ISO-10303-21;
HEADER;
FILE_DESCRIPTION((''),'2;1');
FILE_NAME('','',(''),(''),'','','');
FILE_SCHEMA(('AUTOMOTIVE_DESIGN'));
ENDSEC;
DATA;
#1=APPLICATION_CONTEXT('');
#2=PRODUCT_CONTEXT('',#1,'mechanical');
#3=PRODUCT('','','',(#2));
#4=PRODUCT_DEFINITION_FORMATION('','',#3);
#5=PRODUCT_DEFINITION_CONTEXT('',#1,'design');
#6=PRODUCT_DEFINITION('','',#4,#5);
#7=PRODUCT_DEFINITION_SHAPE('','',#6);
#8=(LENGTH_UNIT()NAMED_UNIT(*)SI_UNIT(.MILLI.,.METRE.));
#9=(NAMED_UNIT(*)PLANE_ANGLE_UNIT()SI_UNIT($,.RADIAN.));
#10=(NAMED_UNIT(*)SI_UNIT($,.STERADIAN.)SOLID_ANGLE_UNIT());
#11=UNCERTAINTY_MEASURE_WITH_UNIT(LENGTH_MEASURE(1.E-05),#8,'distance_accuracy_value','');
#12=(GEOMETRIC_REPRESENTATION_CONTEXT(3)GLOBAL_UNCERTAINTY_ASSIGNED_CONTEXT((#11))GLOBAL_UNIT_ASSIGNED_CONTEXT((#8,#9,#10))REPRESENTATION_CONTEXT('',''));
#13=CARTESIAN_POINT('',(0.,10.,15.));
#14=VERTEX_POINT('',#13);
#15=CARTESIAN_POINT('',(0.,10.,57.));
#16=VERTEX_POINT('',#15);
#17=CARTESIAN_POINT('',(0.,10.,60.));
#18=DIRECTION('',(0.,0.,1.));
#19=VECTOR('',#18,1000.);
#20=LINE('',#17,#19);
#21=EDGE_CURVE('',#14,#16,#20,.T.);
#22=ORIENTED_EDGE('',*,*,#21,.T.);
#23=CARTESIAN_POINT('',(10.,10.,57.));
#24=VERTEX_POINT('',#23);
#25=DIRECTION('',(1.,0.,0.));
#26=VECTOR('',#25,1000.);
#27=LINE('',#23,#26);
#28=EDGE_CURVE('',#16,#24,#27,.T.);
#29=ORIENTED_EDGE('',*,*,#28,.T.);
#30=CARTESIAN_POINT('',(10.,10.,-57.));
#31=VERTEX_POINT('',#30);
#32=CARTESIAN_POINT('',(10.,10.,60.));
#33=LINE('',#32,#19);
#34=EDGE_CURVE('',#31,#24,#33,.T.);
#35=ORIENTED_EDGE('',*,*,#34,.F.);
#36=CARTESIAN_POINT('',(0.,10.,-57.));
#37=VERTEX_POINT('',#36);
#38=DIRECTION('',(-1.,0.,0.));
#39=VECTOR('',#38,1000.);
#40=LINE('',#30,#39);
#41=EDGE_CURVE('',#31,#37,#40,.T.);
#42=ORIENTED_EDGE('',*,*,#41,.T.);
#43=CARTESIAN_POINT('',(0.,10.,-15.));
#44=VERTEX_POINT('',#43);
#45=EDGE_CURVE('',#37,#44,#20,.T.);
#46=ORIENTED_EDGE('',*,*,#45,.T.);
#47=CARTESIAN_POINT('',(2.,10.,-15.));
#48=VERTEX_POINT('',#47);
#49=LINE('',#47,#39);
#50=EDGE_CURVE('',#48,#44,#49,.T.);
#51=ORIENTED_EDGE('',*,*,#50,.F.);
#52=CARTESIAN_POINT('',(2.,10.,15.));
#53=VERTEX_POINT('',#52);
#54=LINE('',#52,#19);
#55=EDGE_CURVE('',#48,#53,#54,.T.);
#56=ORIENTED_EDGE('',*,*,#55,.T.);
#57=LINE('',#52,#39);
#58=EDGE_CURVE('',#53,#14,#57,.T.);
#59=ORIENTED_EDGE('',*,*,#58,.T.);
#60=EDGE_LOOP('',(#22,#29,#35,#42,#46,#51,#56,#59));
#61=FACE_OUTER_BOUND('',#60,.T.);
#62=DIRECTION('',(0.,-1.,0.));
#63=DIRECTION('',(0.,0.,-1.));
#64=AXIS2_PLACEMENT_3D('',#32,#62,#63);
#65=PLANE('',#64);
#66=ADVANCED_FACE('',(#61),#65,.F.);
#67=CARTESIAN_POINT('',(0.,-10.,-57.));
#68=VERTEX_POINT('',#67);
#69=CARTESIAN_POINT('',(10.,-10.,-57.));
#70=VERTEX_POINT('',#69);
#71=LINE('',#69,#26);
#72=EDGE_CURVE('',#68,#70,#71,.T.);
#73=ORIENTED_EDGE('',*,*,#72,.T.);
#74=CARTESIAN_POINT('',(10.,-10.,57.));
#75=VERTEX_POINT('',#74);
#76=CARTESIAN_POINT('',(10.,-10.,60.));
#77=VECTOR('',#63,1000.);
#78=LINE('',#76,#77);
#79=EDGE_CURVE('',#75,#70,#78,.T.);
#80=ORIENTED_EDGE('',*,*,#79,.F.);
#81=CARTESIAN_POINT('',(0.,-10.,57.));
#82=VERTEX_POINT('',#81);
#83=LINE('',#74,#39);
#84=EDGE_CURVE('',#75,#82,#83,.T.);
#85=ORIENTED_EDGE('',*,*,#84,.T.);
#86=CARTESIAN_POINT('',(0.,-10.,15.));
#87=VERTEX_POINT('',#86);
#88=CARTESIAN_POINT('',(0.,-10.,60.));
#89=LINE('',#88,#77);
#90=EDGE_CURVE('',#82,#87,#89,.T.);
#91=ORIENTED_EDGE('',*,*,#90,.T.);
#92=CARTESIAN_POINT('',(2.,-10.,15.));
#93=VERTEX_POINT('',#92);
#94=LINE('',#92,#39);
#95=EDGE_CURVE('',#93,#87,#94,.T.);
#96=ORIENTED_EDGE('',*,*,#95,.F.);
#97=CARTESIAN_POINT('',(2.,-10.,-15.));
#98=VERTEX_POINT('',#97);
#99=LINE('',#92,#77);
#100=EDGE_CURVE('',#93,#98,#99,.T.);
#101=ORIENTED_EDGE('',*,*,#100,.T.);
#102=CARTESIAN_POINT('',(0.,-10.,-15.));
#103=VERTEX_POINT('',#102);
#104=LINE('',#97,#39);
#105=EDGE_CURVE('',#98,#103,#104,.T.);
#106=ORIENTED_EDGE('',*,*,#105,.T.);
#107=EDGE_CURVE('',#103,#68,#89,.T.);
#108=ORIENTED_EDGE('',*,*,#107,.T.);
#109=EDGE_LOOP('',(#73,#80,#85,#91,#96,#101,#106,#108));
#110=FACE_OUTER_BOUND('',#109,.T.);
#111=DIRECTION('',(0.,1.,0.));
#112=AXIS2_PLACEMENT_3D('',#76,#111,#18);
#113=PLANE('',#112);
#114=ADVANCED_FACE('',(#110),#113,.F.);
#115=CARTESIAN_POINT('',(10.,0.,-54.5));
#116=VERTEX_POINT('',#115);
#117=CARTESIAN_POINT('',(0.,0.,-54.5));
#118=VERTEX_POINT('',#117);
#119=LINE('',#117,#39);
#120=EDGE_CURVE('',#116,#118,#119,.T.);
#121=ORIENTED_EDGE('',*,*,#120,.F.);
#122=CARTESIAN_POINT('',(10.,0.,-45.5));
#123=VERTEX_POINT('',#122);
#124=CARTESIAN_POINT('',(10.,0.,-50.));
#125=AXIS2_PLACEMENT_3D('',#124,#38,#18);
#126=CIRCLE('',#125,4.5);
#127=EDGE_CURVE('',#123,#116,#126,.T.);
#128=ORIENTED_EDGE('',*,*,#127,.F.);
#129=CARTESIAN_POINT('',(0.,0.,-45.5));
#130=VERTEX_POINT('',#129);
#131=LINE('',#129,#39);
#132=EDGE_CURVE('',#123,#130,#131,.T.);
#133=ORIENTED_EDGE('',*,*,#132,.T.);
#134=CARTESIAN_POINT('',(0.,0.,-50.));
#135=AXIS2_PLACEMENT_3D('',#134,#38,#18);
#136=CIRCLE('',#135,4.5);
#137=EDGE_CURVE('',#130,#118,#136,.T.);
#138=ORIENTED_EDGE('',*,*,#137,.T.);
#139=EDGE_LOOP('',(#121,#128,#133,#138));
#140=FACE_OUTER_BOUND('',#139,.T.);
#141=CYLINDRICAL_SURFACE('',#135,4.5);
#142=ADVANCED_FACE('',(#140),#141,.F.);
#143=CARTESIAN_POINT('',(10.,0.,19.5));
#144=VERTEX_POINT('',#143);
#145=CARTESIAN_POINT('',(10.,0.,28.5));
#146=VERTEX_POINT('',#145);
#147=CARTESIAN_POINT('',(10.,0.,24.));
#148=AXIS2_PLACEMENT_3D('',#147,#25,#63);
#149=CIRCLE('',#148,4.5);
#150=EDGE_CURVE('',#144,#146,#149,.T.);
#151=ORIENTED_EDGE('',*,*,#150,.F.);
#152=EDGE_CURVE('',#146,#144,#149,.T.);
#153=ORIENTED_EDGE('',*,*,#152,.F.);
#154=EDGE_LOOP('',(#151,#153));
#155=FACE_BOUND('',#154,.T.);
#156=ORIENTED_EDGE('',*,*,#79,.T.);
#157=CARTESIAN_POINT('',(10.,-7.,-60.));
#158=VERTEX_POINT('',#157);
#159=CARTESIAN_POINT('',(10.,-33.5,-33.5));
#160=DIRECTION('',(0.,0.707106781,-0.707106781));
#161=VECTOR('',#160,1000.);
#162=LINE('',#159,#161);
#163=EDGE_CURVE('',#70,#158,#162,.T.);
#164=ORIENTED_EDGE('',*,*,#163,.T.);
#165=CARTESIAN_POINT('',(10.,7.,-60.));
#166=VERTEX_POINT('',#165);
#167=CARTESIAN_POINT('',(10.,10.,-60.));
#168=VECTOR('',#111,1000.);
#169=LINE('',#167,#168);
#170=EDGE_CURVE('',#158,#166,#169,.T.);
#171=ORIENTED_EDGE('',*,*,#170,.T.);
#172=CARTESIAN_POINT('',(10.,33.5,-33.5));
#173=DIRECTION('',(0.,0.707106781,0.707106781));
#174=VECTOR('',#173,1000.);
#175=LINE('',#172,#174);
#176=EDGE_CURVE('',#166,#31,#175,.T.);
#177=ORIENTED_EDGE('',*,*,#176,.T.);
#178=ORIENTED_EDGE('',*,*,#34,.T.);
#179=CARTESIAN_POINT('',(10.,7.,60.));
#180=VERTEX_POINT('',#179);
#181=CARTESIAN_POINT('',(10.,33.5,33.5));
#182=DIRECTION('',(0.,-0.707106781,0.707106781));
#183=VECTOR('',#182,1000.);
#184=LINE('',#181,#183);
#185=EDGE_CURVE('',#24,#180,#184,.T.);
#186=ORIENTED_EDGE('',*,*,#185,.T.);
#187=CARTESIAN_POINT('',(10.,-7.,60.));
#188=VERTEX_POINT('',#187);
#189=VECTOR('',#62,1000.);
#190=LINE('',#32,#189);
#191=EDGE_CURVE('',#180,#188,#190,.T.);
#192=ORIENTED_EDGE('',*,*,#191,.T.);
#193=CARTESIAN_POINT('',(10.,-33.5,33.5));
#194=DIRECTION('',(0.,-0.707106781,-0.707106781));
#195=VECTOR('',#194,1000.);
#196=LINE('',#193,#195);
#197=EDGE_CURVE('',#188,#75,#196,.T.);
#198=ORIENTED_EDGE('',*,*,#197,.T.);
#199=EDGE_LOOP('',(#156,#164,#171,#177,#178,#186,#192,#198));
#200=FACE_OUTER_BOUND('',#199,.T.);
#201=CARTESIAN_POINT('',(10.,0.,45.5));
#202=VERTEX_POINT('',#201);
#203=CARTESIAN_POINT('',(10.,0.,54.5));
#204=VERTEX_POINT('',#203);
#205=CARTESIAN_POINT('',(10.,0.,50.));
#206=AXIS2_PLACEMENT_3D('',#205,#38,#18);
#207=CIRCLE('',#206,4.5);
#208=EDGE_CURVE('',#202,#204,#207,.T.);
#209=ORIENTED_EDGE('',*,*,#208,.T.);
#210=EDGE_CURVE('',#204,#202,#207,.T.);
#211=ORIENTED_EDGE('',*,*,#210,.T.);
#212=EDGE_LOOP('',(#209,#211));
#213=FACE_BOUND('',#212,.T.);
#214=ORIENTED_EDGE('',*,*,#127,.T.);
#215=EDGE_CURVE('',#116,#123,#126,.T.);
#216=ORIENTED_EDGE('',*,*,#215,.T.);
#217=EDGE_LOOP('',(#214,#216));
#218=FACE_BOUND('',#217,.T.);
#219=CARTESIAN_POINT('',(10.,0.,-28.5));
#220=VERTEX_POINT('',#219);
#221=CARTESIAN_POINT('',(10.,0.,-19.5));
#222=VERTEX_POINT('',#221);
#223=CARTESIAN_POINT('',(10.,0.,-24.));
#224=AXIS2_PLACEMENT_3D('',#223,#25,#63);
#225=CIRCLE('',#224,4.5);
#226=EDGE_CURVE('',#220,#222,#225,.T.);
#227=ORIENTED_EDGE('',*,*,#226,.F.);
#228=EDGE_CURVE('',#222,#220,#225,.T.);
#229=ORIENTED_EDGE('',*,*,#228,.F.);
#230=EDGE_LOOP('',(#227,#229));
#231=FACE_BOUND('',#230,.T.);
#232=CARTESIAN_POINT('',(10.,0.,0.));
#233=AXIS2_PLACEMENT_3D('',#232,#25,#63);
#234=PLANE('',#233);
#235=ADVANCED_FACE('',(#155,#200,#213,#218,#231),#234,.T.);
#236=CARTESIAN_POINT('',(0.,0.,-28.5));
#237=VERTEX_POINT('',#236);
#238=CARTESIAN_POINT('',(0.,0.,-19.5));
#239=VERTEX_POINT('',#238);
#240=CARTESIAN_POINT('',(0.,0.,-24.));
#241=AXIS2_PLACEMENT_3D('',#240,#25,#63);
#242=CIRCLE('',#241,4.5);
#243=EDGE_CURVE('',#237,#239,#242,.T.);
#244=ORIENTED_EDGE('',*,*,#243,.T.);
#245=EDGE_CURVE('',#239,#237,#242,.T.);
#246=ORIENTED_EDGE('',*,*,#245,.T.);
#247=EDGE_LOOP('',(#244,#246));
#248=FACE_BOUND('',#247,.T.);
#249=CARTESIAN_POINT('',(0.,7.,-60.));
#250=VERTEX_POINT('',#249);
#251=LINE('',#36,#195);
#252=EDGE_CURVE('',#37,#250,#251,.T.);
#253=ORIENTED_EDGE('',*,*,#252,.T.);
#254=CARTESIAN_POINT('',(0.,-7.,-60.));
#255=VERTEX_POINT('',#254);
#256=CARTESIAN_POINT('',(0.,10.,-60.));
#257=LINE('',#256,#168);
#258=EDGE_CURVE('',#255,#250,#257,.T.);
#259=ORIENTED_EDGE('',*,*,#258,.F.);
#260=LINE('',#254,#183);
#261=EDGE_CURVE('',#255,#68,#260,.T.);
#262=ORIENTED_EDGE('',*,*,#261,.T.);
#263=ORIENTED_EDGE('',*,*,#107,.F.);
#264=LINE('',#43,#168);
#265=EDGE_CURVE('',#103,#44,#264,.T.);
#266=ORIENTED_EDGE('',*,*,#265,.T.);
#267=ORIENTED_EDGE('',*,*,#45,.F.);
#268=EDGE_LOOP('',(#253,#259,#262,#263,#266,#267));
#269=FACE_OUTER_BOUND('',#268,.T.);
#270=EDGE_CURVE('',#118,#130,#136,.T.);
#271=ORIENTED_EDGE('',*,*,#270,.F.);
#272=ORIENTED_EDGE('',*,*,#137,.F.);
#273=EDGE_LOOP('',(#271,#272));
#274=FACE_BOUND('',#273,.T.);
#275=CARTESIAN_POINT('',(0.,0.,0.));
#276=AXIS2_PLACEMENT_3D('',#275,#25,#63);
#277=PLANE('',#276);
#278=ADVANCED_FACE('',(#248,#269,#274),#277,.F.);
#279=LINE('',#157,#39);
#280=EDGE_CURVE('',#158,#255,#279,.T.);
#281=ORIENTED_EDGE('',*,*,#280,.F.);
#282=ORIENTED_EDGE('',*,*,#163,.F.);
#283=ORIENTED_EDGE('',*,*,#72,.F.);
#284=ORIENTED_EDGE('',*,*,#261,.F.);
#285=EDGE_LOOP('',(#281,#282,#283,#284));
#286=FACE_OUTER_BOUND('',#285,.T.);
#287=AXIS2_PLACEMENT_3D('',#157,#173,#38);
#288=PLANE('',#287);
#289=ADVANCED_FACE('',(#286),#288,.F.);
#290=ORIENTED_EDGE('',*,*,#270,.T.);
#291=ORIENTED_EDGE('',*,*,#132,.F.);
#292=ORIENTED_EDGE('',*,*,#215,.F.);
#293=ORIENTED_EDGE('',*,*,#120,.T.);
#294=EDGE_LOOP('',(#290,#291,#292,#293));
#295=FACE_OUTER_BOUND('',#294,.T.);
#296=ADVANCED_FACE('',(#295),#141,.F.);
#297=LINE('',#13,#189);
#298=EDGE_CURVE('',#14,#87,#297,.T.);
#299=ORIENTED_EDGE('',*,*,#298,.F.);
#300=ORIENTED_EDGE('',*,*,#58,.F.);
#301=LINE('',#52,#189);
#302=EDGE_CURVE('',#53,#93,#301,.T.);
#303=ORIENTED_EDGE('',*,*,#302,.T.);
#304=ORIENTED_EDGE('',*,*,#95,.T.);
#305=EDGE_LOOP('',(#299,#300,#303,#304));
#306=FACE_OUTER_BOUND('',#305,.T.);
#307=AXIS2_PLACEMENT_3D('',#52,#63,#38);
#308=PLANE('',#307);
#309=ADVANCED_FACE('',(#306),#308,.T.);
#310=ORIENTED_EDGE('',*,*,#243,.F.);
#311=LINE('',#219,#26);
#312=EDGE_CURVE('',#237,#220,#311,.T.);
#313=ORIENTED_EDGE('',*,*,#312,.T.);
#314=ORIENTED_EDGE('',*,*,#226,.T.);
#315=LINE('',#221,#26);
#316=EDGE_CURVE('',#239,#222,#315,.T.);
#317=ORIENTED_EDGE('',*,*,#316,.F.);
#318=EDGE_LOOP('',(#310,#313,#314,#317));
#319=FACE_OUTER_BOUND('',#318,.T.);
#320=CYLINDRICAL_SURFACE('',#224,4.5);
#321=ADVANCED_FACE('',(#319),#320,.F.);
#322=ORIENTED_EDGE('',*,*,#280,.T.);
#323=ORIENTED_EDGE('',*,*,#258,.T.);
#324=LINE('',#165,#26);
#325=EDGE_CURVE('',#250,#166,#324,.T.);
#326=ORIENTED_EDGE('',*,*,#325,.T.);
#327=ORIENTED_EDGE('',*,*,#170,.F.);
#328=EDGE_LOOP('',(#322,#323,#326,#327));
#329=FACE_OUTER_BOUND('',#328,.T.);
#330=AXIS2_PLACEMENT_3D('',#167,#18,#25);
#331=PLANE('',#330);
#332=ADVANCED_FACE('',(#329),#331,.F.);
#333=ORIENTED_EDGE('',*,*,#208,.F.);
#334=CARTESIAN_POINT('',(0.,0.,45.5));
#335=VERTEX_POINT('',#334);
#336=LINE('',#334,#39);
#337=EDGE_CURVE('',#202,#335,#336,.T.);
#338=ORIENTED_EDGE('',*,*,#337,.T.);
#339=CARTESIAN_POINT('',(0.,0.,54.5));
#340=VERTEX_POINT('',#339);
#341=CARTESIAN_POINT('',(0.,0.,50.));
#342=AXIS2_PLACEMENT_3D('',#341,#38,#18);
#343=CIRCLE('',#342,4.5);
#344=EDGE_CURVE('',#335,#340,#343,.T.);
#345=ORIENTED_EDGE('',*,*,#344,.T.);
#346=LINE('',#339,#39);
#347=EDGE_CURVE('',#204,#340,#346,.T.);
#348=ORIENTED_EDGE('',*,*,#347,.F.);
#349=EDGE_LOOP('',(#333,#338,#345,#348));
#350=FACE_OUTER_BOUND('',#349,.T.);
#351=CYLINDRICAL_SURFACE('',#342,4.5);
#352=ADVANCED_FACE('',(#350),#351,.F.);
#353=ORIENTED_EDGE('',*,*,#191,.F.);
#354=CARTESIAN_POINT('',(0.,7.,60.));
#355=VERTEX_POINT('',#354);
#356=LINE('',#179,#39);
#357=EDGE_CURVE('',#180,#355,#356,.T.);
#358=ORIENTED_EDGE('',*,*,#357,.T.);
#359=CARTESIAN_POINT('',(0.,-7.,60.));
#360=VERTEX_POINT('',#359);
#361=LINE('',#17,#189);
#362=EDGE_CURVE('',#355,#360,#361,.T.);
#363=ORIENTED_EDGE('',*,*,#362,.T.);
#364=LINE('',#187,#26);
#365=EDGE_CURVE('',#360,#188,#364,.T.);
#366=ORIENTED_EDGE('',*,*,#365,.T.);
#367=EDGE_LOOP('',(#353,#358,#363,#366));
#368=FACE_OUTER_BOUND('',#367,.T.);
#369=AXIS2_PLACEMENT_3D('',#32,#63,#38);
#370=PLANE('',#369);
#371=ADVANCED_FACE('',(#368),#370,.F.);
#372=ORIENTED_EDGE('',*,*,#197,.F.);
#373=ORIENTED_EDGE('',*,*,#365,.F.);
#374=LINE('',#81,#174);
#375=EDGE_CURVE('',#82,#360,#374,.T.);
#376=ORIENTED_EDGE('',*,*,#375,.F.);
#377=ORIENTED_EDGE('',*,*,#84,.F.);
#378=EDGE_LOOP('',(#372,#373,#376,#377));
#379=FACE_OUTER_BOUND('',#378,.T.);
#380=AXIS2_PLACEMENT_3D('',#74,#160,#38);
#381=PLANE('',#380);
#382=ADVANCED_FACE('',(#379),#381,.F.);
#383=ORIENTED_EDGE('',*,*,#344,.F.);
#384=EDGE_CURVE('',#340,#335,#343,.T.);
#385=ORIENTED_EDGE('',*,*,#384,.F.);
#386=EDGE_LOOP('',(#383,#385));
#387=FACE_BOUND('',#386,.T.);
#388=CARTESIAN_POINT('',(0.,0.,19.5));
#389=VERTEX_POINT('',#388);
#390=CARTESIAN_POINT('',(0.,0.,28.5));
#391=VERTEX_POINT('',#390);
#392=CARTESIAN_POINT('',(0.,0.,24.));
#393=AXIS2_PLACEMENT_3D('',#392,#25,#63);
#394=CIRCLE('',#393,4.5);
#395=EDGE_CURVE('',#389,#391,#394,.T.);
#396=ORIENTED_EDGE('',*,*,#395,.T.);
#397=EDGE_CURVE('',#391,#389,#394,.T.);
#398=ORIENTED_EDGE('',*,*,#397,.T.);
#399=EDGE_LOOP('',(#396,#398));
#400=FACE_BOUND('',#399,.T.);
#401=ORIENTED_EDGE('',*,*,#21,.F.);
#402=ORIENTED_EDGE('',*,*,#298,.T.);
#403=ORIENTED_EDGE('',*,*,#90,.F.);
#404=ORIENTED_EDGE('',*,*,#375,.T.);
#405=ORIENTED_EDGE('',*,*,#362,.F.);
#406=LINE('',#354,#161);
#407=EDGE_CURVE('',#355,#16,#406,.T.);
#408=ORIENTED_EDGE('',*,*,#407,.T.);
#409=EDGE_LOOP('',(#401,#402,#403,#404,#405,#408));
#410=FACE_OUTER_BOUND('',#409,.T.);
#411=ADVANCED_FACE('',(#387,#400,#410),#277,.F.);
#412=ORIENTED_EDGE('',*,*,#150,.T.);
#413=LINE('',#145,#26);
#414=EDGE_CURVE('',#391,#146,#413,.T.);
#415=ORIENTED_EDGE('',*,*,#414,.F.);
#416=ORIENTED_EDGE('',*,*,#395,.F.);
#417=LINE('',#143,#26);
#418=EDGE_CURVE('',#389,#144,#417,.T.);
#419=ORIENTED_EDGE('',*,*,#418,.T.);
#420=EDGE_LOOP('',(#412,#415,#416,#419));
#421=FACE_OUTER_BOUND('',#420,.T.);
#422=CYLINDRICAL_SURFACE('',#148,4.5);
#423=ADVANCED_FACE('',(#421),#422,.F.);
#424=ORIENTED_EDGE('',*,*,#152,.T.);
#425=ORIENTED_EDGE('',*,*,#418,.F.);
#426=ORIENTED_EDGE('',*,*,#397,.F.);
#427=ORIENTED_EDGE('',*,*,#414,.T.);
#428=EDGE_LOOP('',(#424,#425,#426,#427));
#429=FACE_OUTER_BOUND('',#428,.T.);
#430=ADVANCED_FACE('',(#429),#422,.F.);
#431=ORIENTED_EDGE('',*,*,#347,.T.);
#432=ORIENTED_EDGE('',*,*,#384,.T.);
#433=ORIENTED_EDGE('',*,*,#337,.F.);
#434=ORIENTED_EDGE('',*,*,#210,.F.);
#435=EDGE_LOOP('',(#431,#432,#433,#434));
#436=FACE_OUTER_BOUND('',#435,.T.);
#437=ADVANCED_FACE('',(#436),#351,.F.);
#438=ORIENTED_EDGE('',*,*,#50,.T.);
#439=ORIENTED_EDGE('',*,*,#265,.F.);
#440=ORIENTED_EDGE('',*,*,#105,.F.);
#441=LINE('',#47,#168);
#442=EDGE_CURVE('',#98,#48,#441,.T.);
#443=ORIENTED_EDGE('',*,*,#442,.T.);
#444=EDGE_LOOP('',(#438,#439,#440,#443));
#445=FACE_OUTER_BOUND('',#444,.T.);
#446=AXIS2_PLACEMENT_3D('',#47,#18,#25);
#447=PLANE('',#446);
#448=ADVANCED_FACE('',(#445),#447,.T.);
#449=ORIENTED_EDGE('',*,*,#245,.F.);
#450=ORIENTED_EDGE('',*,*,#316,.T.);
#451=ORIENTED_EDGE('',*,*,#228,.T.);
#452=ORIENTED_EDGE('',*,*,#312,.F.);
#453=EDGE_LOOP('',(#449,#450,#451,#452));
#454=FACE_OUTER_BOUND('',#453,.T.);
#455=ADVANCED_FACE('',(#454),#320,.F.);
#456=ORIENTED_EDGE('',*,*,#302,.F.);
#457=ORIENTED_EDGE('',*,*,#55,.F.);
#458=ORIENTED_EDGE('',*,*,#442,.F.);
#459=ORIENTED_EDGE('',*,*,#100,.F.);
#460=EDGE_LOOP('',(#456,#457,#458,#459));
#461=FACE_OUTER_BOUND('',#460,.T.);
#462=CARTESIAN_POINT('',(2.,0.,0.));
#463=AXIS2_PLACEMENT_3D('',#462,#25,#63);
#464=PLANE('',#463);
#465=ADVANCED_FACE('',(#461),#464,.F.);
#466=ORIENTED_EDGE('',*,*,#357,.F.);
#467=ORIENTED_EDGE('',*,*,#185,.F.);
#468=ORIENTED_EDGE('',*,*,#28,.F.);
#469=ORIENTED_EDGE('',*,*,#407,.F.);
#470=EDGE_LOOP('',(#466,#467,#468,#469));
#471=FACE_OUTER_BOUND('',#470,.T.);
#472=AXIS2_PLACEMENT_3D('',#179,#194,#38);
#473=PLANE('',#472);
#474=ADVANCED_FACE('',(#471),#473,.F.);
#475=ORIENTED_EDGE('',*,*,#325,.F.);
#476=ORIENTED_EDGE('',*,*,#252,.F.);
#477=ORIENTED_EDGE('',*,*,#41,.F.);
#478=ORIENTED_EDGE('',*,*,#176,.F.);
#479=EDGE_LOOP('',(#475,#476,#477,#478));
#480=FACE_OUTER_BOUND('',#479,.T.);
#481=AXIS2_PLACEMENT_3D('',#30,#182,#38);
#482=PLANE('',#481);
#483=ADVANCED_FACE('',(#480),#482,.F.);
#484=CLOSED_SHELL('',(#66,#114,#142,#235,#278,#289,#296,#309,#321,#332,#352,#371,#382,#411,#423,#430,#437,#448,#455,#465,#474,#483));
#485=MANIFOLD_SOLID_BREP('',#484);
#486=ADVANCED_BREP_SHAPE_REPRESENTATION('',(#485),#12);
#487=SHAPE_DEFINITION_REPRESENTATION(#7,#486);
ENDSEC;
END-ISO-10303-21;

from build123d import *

# Parameters (mm, degrees)
SKETCH_1_W            = 120
SKETCH_1_H            = 20
EXTRUDE_1_DEPTH       = 10
HOLE_WIZARD_9_0_9_1_D = 9
HOLE_WIZARD_9_0_9_2_D = 9
SKETCH_6_W            = 30
SKETCH_6_H            = 20
CUT_EXTRUDE_1_DEPTH   = 2
CHAMFER_1_SIZE        = 3


with BuildPart() as part:
    # 草图1 → 凸台-拉伸1 (new body)
    with BuildSketch(Plane(origin=(0, 0, 0), x_dir=(0, 0, -1), z_dir=(1, 0, 0))):
        Rectangle(SKETCH_1_W, SKETCH_1_H)
    extrude(amount=EXTRUDE_1_DEPTH)

    # Ø9.0 (9) 直径孔1 (through all)
    with Locations(Plane(origin=(10, 0, 0), x_dir=(0, 0, -1), z_dir=(1, 0, 0))):
        with Locations((-24, 0), (24, 0)):
            Hole(HOLE_WIZARD_9_0_9_1_D / 2)

    # Ø9.0 (9) 直径孔2 (through all)
    with Locations(Plane.ZY):
        with Locations((-50, 0), (50, 0)):
            Hole(HOLE_WIZARD_9_0_9_2_D / 2)

    # 草图6 → 切除-拉伸1 (cut)
    with BuildSketch(Plane(origin=(0, 0, 0), x_dir=(0, 0, -1), z_dir=(1, 0, 0))):
        Rectangle(SKETCH_6_W, SKETCH_6_H)
    extrude(amount=CUT_EXTRUDE_1_DEPTH, mode=Mode.SUBTRACT)

    # 倒角1
    chamfer_1_edges = [part.edges().sort_by_distance(p)[0] for p in [
        (5, -10, -60),
        (5, -10, 60),
        (5, 10, 60),
        (5, 10, -60),
    ]]
    chamfer(chamfer_1_edges, length=CHAMFER_1_SIZE)


solid = part.part
